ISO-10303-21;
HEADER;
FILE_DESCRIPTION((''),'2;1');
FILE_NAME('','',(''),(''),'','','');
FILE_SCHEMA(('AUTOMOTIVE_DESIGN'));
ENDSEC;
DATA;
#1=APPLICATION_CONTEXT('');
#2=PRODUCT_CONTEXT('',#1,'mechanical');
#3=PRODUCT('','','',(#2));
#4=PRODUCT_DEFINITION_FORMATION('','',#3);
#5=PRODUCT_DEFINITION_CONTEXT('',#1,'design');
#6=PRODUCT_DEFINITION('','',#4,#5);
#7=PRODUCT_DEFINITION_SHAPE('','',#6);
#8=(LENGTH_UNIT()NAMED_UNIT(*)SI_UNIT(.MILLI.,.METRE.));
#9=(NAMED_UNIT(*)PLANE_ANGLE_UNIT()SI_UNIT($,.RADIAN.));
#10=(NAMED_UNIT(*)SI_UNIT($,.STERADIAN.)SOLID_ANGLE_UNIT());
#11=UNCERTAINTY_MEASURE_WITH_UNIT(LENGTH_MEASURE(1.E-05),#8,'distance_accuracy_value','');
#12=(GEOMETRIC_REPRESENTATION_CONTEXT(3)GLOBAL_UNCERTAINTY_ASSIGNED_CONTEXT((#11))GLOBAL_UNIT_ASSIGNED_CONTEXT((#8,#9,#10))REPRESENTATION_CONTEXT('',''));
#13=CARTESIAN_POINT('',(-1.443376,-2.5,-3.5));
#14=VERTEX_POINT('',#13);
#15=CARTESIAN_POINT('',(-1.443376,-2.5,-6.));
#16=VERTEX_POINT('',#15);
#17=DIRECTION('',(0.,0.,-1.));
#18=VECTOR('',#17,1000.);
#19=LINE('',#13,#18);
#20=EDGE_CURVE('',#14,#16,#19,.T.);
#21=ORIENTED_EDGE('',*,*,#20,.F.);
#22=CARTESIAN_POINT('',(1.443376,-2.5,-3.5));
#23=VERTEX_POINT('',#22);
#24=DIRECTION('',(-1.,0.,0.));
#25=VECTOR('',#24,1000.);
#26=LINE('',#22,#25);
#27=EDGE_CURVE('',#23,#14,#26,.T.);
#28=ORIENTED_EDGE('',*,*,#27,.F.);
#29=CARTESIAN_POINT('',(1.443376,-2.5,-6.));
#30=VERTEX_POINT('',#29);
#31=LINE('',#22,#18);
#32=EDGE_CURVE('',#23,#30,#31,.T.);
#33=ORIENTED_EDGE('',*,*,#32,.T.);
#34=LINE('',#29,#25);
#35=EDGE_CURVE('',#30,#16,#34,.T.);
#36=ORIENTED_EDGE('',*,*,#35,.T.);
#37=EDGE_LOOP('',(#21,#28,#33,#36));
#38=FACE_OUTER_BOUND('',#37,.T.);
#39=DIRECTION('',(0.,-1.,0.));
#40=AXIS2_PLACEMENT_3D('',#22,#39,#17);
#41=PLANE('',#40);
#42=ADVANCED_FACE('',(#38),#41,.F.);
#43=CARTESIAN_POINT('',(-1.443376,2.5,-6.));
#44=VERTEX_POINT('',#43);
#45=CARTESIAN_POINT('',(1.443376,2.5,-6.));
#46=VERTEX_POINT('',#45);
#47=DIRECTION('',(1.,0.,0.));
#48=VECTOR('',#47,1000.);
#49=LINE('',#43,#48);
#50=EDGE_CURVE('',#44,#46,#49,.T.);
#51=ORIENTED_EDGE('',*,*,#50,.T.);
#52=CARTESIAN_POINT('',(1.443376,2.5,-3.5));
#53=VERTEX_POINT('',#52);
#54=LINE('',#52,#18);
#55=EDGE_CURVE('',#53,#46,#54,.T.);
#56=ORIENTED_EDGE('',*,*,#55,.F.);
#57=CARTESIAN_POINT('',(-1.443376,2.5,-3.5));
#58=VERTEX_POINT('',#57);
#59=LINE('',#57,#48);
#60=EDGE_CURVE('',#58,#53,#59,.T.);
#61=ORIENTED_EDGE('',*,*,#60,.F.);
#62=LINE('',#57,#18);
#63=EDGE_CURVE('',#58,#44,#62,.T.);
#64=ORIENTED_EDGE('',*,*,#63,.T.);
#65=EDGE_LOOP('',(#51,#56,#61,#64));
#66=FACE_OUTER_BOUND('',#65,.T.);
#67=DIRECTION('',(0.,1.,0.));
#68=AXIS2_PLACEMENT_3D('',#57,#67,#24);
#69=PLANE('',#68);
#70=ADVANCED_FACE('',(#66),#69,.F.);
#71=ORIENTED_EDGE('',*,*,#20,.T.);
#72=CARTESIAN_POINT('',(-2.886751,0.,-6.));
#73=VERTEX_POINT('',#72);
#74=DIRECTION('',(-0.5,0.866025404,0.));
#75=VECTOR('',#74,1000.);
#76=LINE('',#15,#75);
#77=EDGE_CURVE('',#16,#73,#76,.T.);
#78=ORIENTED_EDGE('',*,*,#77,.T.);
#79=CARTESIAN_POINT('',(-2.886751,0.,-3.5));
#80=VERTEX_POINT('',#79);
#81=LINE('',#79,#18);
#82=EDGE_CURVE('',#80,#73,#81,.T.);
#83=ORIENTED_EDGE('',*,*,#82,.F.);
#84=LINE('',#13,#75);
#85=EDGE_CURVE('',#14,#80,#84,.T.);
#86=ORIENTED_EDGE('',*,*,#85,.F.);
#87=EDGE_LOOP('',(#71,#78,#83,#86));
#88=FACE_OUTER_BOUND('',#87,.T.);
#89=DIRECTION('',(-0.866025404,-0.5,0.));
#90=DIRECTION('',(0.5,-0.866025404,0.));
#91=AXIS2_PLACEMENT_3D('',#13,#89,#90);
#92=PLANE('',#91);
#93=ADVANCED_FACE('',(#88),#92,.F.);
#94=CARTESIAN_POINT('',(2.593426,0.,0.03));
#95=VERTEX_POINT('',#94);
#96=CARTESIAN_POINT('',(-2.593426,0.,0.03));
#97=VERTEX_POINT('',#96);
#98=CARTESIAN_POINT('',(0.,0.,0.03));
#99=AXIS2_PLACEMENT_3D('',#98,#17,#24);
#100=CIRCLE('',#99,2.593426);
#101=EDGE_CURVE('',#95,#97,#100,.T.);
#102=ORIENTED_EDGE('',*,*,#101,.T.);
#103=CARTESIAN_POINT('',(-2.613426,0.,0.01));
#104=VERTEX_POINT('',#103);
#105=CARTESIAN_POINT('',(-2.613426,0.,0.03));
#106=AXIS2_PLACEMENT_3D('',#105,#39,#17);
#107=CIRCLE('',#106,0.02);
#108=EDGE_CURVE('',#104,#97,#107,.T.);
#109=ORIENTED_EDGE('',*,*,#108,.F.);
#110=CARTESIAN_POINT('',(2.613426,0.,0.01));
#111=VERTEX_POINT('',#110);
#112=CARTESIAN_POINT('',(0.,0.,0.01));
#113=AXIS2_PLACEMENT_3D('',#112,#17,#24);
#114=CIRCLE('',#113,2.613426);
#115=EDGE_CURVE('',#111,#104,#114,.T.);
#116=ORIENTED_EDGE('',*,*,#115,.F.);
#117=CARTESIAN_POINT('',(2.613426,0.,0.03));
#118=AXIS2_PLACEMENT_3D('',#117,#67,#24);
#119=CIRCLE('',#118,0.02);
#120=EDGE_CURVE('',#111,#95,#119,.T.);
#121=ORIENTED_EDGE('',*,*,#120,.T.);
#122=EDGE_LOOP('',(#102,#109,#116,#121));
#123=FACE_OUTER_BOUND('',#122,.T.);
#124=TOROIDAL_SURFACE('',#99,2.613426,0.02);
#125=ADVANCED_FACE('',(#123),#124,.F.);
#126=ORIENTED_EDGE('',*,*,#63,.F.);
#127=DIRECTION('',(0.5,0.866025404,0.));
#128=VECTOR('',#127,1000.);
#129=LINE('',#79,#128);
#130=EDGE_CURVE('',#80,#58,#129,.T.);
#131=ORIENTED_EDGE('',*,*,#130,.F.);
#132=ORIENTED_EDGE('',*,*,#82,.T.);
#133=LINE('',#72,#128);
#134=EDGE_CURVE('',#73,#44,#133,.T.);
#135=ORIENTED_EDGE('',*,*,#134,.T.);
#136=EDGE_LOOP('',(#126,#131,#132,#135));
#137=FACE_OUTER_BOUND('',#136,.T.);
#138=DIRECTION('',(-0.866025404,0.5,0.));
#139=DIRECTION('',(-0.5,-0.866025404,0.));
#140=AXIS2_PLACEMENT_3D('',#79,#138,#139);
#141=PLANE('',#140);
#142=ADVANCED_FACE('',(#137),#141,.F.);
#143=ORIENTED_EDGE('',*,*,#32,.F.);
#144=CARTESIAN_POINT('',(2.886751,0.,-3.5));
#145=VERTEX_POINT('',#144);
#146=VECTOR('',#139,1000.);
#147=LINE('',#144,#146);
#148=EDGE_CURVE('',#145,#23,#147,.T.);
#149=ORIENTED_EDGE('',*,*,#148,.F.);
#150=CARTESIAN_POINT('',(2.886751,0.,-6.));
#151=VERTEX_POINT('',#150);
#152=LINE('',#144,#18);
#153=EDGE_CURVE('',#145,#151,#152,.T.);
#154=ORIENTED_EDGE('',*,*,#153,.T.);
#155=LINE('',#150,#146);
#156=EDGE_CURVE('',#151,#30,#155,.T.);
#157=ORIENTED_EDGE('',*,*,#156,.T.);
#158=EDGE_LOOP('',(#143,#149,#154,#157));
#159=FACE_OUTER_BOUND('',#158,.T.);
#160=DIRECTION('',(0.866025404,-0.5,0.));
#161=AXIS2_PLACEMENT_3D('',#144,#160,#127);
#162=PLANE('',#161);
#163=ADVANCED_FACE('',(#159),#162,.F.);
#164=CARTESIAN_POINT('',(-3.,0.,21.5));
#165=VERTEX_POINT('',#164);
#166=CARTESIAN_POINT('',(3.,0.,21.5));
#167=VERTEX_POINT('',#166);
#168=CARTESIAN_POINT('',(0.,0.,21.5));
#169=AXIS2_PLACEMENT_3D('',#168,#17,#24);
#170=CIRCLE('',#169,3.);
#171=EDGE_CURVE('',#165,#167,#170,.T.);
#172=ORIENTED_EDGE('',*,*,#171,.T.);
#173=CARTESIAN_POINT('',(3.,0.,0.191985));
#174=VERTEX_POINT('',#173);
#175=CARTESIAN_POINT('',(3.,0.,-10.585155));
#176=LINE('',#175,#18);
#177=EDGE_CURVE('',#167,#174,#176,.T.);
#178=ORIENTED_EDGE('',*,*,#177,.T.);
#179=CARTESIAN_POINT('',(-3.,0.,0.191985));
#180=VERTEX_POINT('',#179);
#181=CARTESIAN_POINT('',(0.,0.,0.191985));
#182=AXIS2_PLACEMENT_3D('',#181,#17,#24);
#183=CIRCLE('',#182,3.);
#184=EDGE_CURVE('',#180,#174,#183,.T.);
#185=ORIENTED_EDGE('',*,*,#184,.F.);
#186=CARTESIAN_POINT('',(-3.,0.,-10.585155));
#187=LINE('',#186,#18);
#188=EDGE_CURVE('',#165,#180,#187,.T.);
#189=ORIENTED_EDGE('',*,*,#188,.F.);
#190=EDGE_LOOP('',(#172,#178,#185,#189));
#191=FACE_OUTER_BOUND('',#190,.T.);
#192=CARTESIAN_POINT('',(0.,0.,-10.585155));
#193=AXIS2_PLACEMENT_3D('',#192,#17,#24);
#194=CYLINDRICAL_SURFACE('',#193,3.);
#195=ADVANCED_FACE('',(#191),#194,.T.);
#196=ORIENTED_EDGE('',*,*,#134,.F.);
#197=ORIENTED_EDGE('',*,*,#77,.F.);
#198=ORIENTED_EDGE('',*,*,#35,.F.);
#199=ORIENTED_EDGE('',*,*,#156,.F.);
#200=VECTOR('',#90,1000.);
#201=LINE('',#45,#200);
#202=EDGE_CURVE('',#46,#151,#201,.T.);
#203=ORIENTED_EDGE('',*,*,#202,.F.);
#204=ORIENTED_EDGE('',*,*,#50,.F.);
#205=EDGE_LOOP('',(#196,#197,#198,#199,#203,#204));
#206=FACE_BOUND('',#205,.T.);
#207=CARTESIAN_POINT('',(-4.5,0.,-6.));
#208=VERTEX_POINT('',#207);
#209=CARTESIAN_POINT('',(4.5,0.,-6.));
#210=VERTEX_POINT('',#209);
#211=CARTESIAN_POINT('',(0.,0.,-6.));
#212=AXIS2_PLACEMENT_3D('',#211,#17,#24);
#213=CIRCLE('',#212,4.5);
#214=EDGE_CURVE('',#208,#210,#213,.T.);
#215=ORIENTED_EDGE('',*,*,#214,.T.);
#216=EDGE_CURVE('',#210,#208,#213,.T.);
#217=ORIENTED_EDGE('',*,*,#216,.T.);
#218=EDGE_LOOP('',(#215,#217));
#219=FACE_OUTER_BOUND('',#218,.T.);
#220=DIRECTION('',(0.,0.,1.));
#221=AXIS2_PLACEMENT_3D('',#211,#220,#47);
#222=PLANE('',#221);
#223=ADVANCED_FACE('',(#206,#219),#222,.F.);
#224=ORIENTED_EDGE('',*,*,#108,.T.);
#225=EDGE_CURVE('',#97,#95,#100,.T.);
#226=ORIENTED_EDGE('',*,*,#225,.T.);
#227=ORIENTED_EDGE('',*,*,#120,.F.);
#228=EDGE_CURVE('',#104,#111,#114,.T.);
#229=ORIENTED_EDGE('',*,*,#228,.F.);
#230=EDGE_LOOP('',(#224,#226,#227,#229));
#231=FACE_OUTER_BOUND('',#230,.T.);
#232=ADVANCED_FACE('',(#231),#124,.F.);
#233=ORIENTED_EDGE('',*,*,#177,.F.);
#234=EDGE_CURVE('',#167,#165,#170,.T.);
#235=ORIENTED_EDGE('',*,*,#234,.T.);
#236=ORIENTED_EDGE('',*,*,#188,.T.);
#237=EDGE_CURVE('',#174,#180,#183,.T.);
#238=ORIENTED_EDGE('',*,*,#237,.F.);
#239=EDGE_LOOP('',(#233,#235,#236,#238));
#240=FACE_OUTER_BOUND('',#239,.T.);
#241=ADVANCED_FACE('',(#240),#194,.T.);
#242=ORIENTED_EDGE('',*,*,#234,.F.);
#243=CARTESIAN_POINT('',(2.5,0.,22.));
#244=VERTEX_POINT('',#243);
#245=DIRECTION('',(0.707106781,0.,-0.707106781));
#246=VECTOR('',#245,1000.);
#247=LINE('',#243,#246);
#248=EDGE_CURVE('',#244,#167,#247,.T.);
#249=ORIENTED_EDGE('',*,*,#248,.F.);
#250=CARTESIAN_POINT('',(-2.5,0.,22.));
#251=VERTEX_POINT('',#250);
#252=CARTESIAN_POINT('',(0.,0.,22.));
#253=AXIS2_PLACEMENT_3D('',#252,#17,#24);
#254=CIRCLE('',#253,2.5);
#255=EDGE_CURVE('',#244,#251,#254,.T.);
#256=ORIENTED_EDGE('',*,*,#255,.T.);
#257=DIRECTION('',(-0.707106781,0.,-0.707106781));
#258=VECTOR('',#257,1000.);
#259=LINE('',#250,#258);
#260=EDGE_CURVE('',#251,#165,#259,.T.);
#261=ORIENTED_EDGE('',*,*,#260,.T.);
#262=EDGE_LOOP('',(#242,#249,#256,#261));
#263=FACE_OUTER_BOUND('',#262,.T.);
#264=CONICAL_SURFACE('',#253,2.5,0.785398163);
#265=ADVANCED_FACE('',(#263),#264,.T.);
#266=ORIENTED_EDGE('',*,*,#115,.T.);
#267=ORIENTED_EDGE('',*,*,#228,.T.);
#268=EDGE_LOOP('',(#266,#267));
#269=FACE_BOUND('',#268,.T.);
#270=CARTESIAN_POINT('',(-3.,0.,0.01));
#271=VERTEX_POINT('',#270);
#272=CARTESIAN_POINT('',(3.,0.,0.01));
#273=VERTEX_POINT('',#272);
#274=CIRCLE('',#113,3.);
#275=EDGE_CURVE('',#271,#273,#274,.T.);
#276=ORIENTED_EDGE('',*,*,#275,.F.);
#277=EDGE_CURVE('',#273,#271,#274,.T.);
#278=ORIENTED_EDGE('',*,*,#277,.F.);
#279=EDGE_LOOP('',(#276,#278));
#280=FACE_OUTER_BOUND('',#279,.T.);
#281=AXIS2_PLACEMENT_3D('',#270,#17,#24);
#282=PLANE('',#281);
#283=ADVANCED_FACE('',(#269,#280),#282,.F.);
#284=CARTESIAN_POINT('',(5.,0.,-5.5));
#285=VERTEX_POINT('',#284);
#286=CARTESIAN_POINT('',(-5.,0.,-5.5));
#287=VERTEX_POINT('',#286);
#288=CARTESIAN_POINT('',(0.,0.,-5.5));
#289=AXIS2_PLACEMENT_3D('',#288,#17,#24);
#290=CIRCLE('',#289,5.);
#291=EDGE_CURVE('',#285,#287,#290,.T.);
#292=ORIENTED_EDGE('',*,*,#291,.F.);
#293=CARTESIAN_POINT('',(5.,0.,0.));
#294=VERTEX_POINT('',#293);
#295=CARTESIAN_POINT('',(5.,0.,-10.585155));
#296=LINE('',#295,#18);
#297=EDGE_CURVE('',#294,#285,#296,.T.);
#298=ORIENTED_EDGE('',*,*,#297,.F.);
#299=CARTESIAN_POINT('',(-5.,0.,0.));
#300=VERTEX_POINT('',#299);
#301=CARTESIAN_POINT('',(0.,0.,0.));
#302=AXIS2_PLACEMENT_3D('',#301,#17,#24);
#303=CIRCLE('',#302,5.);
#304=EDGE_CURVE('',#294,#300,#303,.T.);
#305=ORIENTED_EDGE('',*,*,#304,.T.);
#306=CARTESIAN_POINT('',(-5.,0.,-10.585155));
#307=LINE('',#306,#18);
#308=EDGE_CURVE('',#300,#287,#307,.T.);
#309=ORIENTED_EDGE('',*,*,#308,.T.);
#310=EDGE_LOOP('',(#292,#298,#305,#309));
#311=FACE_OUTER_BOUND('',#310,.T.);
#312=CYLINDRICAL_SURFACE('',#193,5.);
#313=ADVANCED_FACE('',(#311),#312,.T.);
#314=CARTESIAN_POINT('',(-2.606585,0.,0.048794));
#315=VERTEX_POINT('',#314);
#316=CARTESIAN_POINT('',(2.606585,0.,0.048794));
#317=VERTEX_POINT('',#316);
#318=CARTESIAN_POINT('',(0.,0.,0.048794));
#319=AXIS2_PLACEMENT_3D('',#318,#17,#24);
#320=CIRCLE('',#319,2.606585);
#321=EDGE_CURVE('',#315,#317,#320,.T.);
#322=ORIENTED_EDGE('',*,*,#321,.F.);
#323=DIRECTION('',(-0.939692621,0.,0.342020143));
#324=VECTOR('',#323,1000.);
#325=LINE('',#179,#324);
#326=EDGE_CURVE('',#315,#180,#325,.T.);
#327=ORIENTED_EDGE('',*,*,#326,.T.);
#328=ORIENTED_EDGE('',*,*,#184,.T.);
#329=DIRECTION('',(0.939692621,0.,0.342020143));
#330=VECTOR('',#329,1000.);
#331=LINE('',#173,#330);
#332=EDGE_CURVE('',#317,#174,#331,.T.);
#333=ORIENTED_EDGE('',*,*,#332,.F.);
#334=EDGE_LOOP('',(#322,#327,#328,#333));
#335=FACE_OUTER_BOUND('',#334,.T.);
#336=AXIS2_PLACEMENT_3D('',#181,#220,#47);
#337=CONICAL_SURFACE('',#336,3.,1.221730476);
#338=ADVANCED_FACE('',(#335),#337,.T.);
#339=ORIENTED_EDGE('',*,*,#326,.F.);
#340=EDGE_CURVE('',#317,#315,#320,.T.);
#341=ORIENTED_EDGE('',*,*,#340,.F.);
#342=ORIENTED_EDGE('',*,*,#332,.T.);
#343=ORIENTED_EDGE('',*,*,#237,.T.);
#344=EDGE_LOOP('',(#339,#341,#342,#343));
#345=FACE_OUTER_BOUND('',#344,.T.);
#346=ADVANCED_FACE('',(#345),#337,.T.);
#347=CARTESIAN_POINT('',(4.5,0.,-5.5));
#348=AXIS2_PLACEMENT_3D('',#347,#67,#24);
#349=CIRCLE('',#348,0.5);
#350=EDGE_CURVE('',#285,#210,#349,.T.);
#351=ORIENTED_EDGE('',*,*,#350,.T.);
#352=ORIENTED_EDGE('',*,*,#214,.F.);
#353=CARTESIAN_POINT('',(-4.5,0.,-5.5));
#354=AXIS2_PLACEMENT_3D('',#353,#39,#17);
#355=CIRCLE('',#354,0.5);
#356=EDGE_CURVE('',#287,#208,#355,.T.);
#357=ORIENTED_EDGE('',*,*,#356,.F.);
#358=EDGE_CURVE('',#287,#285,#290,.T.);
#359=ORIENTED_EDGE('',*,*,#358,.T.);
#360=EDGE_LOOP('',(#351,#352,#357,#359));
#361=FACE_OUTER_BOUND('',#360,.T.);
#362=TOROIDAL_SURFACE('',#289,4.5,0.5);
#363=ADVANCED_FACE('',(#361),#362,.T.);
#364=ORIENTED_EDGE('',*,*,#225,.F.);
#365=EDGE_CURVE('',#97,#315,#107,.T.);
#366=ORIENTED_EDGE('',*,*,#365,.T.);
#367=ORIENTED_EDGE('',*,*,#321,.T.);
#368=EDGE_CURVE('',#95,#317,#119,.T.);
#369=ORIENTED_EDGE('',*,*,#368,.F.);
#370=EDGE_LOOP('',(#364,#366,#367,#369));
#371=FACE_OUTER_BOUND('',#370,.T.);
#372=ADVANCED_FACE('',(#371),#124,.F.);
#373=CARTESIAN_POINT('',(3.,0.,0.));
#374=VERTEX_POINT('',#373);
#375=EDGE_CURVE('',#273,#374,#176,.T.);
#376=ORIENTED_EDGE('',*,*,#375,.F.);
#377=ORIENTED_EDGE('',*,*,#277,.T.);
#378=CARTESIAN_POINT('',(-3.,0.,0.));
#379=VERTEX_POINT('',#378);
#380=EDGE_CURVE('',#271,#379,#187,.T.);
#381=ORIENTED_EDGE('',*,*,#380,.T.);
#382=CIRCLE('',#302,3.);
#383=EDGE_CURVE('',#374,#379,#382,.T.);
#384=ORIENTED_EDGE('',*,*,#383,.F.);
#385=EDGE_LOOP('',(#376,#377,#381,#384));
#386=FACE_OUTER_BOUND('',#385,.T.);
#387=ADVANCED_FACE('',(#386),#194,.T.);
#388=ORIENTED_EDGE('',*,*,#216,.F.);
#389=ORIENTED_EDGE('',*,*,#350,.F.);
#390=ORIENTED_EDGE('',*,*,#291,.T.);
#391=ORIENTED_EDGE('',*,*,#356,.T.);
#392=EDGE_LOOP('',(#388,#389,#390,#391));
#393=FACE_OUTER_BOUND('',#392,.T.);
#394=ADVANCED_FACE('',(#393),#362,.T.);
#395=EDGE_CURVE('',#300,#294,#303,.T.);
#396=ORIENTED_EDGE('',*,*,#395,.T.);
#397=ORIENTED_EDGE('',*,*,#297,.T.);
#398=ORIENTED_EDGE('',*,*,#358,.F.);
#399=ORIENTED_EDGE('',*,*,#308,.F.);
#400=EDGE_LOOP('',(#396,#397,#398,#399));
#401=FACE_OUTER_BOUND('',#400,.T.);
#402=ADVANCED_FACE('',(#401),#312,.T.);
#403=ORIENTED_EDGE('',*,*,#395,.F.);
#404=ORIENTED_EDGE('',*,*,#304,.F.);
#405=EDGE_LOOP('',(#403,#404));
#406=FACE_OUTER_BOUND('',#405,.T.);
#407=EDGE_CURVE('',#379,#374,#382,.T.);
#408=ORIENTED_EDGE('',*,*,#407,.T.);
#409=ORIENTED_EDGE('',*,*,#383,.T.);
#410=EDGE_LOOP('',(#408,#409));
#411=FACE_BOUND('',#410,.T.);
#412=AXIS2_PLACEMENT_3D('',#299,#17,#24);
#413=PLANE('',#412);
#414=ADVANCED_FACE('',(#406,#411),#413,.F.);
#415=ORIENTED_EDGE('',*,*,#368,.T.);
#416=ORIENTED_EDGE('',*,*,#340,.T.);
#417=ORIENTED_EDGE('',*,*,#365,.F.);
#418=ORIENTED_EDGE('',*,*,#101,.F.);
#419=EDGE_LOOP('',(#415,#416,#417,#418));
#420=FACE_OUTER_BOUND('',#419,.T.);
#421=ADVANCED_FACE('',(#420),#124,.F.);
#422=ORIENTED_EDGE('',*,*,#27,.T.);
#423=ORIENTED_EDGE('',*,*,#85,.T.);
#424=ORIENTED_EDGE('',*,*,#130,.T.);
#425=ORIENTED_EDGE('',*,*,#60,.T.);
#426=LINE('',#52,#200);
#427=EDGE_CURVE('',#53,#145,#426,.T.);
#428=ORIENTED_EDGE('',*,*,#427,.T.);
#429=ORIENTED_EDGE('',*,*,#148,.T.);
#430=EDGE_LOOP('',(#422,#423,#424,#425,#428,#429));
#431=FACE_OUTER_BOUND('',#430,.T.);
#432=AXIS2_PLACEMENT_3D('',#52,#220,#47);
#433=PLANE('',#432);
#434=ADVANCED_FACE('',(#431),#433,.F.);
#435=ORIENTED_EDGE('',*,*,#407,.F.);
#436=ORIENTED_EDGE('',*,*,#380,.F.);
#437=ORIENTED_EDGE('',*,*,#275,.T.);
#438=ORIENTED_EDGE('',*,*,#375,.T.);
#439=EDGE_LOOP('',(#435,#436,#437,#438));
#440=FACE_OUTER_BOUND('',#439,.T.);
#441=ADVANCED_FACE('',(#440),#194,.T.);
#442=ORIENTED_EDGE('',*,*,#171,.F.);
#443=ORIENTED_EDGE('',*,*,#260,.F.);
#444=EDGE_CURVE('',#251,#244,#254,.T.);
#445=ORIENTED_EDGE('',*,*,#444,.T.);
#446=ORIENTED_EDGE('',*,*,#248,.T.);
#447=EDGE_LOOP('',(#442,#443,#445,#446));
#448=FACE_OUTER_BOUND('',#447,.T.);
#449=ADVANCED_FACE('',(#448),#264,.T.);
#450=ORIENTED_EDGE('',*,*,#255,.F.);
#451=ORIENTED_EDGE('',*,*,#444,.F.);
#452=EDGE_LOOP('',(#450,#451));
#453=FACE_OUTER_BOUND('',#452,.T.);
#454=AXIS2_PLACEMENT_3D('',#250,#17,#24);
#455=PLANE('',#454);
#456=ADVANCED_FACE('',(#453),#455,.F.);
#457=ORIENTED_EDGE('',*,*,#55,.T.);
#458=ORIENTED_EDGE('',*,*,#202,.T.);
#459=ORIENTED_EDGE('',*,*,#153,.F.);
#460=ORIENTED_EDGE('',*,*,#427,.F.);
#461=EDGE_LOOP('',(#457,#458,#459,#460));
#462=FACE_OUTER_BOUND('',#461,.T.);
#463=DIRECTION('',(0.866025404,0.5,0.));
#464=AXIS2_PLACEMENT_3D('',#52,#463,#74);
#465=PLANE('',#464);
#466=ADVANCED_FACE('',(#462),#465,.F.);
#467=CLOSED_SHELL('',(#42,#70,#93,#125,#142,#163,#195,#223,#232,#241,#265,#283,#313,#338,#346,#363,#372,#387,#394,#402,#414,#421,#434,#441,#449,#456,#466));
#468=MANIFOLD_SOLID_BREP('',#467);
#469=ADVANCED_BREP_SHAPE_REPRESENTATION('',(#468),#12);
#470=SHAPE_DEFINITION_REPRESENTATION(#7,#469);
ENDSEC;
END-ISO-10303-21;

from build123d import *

# Parameters (mm, degrees)
CUT_EXTRUDE1_DEPTH = 2.5


with BuildPart() as part:
    # Logo3_bib1 → Revolve1 (revolve)
    with BuildSketch(Plane(origin=(0, 0, 0), x_dir=(-1, 0, 0), z_dir=(0, -1, 0))):
        with BuildLine():
            Line((0, -22), (0, 6))
            Line((0, 6), (4.5, 6))
            ThreePointArc((4.5, 6), (4.853553391, 5.853553391), (5, 5.5))
            Line((5, 5.5), (5, 0))
            Line((5, 0), (3, 0))
            Line((3, 0), (3, -0.01))
            Line((3, -0.01), (2.613425636, -0.01))
            ThreePointArc((2.613425636, -0.01), (2.593729481, -0.026527036), (2.606585234, -0.048793852))
            Line((2.606585234, -0.048793852), (3, -0.191985117))
            Line((3, -0.191985117), (3, -21.5))
            Line((3, -21.5), (2.5, -22))
            Line((2.5, -22), (0, -22))
        make_face()
    revolve(axis=Axis((0, 0, -10.585154653), (0, 0, 1)))

    # Logo3_bib2 → Cut-Extrude1 (cut)
    with BuildSketch(Plane(origin=(0, 0, -6), x_dir=(1, 0, 0), z_dir=(0, 0, -1))):
        Polygon((2.886751346, 0), (1.443375673, 2.5), (-1.443375673, 2.5), (-2.886751346, 0), (-1.443375673, -2.5), (1.443375673, -2.5), align=None)
    extrude(amount=-CUT_EXTRUDE1_DEPTH, mode=Mode.SUBTRACT)


solid = part.part
